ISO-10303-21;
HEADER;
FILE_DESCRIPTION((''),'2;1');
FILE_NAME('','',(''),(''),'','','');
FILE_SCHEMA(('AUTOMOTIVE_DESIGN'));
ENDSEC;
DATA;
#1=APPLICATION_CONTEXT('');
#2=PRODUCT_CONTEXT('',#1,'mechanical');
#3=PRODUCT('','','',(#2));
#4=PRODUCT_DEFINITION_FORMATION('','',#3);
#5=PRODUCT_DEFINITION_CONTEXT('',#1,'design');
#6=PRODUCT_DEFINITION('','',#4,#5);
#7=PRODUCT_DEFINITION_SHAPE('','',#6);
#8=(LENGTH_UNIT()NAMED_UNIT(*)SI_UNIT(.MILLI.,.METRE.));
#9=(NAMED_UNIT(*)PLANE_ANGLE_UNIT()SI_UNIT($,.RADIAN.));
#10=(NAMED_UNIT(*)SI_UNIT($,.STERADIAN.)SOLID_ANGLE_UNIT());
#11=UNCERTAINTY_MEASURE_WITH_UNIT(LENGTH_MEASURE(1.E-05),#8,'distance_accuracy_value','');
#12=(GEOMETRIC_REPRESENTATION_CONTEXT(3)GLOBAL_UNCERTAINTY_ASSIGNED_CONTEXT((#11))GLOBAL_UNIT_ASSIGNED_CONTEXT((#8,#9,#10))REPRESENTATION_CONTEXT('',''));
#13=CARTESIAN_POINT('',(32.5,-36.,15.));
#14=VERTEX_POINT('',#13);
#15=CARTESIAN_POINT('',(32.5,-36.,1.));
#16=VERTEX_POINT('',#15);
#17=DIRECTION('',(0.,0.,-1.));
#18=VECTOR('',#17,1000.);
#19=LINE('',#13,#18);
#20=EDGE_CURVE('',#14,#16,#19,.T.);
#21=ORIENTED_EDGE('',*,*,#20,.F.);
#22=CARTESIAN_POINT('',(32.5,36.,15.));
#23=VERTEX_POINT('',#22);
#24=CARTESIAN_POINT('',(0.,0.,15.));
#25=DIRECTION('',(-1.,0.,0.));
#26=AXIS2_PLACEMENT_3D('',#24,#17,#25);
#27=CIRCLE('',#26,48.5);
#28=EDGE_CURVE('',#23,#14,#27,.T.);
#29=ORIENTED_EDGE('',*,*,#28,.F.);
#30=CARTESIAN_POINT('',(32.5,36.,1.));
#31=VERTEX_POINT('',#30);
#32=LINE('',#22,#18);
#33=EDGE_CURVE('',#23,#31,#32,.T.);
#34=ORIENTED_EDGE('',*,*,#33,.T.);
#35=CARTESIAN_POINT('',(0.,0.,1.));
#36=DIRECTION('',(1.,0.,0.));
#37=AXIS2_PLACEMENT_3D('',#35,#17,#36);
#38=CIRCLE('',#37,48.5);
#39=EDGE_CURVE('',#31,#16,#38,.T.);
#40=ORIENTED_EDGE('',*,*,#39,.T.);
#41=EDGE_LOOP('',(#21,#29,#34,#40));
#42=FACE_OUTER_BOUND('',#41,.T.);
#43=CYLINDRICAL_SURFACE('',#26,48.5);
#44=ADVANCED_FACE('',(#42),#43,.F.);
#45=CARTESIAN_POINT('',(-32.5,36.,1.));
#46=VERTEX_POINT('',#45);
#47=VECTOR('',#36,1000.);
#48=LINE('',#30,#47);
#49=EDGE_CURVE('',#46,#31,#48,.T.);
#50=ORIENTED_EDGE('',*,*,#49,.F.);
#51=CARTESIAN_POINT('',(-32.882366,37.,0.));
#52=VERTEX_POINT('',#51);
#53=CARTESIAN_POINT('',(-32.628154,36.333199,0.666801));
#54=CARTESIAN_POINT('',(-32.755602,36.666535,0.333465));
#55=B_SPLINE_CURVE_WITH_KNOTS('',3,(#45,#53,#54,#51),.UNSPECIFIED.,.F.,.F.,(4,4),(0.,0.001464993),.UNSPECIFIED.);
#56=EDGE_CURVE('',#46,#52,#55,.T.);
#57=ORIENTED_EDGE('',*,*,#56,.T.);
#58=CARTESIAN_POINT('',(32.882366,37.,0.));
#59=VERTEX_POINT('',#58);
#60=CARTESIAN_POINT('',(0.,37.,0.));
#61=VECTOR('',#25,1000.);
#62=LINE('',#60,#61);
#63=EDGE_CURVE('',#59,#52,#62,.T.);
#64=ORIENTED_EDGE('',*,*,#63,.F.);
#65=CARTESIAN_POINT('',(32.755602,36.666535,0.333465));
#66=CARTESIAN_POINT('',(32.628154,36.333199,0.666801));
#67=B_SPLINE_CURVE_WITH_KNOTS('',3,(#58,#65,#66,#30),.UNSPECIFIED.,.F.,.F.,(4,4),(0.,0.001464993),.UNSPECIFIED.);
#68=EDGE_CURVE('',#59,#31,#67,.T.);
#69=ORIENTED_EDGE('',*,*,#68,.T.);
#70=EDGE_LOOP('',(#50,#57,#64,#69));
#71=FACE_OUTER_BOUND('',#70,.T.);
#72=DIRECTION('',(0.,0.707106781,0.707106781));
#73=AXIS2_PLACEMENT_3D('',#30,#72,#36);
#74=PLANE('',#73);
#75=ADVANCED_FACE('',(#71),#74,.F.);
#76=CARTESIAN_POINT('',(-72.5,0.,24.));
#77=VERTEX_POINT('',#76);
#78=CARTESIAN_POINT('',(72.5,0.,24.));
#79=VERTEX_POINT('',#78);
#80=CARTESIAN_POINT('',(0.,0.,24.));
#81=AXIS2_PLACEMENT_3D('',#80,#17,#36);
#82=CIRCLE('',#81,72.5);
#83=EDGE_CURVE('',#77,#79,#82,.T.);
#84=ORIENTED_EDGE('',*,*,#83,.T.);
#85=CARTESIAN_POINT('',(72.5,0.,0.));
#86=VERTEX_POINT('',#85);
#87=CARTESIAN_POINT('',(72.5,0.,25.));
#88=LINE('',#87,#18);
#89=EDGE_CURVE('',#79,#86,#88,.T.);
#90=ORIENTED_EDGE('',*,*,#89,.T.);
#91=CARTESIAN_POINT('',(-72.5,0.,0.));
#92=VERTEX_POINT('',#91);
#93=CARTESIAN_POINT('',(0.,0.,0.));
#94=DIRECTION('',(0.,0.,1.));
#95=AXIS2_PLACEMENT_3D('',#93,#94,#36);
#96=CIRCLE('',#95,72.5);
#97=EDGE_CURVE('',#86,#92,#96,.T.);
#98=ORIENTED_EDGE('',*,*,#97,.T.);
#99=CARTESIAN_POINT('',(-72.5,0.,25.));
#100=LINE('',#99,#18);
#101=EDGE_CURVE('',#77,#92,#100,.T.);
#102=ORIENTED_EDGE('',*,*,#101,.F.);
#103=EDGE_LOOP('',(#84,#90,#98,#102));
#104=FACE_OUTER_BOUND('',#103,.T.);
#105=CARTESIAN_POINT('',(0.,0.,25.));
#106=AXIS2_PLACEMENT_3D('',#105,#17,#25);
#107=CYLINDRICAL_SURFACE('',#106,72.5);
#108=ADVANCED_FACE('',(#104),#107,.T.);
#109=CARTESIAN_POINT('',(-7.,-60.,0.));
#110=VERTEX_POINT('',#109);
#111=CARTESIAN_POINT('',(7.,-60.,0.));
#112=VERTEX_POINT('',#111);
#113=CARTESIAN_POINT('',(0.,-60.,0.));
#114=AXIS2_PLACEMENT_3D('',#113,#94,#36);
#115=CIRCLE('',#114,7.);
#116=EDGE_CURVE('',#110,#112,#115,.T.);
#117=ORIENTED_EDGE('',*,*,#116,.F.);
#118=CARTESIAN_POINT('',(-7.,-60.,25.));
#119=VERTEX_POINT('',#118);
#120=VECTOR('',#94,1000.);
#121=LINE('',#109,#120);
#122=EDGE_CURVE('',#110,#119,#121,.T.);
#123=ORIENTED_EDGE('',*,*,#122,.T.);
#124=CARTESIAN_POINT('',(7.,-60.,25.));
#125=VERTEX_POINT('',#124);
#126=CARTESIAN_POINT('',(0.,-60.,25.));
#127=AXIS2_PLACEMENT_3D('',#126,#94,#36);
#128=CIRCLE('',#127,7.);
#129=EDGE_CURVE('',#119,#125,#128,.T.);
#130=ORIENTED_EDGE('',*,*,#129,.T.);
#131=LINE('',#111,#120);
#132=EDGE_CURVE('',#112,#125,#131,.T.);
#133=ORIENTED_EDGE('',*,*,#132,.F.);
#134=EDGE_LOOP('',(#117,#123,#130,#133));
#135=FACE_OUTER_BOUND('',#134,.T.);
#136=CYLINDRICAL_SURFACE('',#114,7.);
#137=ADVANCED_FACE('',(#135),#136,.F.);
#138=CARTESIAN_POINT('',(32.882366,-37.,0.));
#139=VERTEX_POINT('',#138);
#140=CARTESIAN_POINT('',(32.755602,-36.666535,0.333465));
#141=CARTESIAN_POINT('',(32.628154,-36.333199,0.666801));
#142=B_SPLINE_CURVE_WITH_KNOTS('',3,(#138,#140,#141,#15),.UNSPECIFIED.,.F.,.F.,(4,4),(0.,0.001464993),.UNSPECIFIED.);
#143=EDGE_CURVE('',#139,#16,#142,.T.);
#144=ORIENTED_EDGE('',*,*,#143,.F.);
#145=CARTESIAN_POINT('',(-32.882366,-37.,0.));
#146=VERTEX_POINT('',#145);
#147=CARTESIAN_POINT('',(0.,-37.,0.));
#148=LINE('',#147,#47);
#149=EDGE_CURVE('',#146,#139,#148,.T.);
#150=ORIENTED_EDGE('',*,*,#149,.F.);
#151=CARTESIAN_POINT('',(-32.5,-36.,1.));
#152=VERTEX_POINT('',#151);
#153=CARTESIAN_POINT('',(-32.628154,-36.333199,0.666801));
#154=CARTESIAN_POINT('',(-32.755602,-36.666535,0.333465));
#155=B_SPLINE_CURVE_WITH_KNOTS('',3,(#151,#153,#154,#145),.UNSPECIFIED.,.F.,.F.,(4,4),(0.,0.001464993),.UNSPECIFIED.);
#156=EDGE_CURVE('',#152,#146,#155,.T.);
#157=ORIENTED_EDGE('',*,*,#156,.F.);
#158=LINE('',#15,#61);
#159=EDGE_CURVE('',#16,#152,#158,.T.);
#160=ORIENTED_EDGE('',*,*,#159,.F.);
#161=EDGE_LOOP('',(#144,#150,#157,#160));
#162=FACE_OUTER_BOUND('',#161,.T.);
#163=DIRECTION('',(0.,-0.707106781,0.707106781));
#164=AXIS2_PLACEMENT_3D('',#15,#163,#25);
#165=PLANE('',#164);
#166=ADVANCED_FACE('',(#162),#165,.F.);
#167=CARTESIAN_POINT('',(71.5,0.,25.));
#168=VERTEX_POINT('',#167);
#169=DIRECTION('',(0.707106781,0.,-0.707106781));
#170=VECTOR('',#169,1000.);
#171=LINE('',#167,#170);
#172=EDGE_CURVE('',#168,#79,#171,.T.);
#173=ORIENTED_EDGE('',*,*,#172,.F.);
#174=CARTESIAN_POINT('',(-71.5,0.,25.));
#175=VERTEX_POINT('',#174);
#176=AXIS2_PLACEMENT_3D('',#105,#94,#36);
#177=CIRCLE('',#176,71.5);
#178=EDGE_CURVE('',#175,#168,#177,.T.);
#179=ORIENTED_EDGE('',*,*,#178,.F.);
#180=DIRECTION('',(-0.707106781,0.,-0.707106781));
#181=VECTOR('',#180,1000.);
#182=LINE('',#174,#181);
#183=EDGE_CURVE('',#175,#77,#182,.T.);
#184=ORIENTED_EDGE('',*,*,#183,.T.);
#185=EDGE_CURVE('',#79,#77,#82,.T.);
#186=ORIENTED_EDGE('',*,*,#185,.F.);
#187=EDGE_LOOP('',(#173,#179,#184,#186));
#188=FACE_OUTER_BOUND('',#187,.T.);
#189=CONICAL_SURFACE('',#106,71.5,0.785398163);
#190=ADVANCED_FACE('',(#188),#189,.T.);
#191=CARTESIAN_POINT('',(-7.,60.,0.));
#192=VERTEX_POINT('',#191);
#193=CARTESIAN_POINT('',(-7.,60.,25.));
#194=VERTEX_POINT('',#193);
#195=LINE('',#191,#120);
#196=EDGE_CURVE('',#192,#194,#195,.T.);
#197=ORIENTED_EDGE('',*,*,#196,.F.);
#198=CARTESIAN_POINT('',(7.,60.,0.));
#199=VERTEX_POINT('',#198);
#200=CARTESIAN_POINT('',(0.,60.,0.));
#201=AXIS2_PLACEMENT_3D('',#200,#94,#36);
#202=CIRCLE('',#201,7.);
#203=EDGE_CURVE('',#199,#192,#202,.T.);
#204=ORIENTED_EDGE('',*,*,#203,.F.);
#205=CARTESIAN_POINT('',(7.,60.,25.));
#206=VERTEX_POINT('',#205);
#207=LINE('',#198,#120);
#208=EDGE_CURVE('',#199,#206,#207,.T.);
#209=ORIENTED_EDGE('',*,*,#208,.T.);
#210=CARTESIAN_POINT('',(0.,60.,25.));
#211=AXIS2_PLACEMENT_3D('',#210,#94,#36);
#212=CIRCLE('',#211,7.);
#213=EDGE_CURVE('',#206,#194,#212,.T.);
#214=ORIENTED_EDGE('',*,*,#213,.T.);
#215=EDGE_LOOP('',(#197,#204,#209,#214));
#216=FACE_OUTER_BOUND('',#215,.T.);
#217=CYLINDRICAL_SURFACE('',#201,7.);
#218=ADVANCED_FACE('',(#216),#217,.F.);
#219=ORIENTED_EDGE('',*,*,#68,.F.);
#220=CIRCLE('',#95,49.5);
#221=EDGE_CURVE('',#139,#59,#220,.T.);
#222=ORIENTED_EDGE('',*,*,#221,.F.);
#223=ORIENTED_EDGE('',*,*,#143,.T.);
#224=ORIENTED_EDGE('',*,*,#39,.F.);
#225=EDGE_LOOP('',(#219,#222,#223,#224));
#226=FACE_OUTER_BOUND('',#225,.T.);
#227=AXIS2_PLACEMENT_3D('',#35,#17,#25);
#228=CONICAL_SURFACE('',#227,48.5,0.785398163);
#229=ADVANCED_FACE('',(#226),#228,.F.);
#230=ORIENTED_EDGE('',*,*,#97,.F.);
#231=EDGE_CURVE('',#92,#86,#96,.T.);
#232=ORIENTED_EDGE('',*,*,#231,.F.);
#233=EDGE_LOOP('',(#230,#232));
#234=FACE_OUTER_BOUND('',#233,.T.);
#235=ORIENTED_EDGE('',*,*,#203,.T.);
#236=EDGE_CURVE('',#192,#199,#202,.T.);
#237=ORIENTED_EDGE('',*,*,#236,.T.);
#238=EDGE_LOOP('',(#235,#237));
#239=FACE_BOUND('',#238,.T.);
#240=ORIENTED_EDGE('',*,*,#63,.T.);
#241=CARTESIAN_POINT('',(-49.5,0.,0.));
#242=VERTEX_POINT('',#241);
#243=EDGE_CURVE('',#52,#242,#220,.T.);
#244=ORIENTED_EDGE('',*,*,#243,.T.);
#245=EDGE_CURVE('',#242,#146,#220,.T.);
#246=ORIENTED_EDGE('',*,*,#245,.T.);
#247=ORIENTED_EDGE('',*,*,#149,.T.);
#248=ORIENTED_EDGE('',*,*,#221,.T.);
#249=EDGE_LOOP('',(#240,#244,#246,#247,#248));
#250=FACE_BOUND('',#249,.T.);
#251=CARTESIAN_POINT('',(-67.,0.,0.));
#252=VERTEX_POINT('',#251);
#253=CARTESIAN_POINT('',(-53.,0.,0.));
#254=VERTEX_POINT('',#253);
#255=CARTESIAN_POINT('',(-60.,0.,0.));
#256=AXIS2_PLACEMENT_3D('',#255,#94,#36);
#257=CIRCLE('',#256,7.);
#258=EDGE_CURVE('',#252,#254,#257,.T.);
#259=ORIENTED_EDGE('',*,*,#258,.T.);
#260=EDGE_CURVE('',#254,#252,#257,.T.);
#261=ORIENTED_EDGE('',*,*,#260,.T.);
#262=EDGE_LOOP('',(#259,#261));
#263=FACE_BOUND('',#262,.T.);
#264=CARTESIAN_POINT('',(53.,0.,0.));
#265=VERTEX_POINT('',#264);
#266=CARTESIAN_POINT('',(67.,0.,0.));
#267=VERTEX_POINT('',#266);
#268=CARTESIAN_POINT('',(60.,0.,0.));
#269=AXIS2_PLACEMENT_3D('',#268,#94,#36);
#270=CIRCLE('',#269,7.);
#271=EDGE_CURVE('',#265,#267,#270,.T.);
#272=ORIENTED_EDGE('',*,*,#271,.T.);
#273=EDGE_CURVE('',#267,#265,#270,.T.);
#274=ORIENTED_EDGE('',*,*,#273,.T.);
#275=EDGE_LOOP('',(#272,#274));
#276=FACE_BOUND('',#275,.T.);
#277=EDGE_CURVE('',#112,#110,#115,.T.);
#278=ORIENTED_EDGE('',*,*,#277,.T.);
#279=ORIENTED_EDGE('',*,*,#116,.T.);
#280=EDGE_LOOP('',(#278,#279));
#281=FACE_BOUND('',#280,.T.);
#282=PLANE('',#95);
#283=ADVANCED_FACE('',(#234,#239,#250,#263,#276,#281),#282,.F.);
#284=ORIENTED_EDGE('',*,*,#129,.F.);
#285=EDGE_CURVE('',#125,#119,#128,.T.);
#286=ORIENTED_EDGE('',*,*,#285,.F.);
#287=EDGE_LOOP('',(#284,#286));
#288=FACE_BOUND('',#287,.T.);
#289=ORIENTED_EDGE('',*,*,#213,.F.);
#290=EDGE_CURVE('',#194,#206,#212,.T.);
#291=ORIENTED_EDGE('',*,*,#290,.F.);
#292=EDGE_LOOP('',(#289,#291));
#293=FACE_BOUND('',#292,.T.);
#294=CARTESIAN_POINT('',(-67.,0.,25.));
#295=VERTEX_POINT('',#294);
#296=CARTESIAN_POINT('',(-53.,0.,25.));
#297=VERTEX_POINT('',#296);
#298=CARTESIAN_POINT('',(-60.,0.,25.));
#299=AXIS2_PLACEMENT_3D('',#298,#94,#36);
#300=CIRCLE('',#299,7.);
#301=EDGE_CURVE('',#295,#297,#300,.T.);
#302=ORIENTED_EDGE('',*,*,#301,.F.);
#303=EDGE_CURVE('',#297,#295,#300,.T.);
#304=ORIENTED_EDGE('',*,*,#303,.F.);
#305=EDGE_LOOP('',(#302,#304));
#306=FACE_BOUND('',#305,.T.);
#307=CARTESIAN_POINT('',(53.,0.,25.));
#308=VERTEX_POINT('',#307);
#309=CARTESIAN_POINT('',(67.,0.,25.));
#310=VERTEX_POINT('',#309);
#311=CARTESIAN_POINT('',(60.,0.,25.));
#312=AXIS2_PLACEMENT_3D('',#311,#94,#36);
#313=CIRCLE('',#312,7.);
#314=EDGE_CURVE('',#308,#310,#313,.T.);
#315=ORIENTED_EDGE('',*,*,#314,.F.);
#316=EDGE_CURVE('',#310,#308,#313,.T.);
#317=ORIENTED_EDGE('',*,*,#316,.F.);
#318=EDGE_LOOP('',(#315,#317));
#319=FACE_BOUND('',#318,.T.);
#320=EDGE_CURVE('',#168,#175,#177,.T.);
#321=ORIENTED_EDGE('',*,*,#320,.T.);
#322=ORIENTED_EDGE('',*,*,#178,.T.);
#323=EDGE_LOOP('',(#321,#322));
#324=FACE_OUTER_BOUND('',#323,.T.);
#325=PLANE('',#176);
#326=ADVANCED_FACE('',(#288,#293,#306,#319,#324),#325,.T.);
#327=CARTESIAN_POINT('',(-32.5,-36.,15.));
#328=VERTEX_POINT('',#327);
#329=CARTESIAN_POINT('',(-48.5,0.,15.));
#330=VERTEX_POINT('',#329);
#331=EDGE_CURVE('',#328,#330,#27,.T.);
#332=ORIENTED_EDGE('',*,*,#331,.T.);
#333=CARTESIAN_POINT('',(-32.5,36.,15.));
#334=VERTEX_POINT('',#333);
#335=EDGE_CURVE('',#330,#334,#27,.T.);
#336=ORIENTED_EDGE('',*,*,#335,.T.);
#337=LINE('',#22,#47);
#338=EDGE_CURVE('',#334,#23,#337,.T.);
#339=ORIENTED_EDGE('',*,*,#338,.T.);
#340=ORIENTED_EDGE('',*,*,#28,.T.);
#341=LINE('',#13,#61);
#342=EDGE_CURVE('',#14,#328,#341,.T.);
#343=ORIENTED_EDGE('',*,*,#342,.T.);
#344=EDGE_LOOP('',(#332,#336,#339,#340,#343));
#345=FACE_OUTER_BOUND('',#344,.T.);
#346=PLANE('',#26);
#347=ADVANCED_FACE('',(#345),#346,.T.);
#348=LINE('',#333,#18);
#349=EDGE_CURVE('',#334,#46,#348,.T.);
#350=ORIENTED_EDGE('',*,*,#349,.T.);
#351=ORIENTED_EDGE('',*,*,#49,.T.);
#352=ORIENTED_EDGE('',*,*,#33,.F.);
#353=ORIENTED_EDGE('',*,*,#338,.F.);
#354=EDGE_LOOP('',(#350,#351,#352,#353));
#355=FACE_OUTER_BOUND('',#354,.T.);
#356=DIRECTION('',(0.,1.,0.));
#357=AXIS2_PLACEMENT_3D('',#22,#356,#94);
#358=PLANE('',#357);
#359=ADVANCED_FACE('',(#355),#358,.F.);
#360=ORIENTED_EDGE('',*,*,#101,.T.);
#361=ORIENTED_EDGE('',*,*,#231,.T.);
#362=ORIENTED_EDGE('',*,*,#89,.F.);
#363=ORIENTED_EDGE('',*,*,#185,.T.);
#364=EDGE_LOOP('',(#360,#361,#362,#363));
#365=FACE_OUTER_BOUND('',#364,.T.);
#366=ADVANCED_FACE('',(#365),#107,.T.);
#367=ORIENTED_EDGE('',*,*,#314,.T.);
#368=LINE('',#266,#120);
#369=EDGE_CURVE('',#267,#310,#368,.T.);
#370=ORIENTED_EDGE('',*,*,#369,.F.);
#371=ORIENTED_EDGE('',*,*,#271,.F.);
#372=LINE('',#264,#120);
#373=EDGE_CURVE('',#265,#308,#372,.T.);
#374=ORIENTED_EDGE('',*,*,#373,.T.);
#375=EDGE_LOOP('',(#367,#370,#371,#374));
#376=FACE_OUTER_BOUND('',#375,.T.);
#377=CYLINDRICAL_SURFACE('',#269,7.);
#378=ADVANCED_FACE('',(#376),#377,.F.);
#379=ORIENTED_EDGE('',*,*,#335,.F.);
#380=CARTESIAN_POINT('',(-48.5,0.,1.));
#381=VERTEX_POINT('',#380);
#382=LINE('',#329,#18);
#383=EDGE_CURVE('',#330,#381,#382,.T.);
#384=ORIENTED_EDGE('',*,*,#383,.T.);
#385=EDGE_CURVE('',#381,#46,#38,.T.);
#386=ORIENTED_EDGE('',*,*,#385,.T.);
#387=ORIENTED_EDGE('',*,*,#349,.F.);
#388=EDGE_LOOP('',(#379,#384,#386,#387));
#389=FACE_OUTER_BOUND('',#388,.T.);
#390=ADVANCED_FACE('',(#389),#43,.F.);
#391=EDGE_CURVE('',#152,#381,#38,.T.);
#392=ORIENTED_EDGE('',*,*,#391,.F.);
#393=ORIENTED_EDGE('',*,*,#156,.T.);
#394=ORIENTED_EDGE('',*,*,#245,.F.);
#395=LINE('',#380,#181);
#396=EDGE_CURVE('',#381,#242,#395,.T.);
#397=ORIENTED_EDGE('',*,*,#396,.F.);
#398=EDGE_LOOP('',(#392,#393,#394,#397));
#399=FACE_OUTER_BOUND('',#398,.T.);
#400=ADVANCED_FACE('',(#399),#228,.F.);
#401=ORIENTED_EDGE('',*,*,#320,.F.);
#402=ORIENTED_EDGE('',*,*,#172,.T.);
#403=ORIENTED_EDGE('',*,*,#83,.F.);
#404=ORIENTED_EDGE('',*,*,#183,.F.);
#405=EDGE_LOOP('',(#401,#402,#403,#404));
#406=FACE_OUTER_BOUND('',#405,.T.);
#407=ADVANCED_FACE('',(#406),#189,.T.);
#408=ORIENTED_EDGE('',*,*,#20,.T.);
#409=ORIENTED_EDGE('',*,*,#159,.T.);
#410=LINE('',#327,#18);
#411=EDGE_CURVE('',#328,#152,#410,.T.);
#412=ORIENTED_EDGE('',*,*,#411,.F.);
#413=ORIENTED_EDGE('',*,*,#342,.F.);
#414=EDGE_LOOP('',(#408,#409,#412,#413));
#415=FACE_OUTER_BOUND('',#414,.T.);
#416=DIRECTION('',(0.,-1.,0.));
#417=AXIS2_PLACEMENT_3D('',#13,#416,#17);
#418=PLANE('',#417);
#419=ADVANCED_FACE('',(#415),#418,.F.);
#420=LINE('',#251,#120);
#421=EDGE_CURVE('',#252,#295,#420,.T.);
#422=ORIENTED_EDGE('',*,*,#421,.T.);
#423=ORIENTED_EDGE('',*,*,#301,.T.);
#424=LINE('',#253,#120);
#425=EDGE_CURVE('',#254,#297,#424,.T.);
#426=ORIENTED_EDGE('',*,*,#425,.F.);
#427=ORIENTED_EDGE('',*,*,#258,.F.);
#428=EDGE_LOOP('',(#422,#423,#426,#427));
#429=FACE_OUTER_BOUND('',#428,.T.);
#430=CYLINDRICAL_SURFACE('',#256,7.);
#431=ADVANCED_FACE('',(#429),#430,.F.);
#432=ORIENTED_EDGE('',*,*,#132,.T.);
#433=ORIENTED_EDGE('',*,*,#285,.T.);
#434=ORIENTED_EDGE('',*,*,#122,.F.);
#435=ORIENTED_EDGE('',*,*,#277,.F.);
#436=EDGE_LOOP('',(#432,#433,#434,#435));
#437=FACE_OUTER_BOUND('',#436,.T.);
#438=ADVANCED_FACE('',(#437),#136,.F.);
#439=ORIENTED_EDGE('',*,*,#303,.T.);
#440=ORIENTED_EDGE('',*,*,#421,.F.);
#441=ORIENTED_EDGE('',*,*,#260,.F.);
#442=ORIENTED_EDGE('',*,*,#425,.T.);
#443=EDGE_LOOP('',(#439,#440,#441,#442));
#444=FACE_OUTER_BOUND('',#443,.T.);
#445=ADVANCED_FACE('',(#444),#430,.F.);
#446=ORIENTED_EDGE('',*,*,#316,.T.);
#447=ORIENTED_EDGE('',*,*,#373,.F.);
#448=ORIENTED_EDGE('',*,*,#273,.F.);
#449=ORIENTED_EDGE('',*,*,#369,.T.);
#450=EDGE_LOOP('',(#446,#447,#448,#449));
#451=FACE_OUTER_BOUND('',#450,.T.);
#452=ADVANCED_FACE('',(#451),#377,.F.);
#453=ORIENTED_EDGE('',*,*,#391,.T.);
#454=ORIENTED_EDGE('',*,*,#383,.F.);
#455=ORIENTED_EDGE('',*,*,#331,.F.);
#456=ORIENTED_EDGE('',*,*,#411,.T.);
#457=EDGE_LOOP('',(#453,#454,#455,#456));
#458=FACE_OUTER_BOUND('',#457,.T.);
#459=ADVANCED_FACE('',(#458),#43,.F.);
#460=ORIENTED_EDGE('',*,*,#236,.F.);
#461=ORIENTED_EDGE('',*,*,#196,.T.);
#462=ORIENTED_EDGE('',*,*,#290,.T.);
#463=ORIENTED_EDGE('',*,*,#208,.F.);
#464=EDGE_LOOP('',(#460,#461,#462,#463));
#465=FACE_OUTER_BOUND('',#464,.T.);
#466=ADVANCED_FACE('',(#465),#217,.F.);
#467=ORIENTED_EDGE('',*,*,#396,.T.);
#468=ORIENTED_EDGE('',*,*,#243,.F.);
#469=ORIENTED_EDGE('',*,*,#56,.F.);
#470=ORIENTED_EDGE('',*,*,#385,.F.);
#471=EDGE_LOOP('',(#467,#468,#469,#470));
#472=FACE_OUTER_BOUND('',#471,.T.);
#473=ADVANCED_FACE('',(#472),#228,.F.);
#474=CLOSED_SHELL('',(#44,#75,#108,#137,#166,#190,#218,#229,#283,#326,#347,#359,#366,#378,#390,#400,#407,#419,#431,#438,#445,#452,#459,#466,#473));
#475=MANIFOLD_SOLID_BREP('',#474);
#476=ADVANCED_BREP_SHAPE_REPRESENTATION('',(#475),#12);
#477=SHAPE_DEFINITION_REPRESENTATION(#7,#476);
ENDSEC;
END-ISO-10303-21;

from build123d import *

# Parameters (mm, degrees)
SKETCH_1_R          = 72.5
EXTRUDE_1_DEPTH     = 25
SKETCH_2_R          = 7
CUT_EXTRUDE_1_DEPTH = 106.534354596
CUT_EXTRUDE_2_DEPTH = 15
CHAMFER_1_SIZE      = 1
CHAMFER_2_SIZE      = 1


with BuildPart() as part:
    # 草图1 → 凸台-拉伸1 (new body)
    with BuildSketch(Plane.XY):
        Circle(SKETCH_1_R)
    extrude(amount=EXTRUDE_1_DEPTH)

    # 草图2 → 切除-拉伸1 (cut, through all)
    with BuildSketch(Plane.XY.offset(25)):
        with Locations((0, 60)):
            Circle(SKETCH_2_R)
        with Locations((60, 0)):
            Circle(SKETCH_2_R)
        with Locations((0, -60)):
            Circle(SKETCH_2_R)
        with Locations((-60, 0)):
            Circle(SKETCH_2_R)
    extrude(amount=-CUT_EXTRUDE_1_DEPTH, mode=Mode.SUBTRACT)

    # 草图3 → 切除-拉伸2 (cut)
    with BuildSketch(Plane(origin=(0, 0, 0), x_dir=(-1, 0, 0), z_dir=(0, 0, -1))):
        with BuildLine():
            Line((-32.5, 36), (32.5, 36))
            ThreePointArc((32.5, 36), (48.5, 0), (32.5, -36))
            Line((32.5, -36), (-32.5, -36))
            ThreePointArc((-32.5, -36), (-48.5, 0), (-32.5, 36))
        make_face()
    extrude(amount=-CUT_EXTRUDE_2_DEPTH, mode=Mode.SUBTRACT)

    # 倒角1
    chamfer_1_edges = [part.edges().sort_by_distance(p)[0] for p in [
        (-72.5, 0, 25),
    ]]
    chamfer(chamfer_1_edges, length=CHAMFER_1_SIZE)

    # 倒角2
    chamfer_2_edges = [part.edges().sort_by_distance(p)[0] for p in [
        (48.5, 0, 0),
        (0, -36, 0),
        (-48.5, 0, 0),
        (0, 36, 0),
    ]]
    chamfer(chamfer_2_edges, length=CHAMFER_2_SIZE)


solid = part.part
